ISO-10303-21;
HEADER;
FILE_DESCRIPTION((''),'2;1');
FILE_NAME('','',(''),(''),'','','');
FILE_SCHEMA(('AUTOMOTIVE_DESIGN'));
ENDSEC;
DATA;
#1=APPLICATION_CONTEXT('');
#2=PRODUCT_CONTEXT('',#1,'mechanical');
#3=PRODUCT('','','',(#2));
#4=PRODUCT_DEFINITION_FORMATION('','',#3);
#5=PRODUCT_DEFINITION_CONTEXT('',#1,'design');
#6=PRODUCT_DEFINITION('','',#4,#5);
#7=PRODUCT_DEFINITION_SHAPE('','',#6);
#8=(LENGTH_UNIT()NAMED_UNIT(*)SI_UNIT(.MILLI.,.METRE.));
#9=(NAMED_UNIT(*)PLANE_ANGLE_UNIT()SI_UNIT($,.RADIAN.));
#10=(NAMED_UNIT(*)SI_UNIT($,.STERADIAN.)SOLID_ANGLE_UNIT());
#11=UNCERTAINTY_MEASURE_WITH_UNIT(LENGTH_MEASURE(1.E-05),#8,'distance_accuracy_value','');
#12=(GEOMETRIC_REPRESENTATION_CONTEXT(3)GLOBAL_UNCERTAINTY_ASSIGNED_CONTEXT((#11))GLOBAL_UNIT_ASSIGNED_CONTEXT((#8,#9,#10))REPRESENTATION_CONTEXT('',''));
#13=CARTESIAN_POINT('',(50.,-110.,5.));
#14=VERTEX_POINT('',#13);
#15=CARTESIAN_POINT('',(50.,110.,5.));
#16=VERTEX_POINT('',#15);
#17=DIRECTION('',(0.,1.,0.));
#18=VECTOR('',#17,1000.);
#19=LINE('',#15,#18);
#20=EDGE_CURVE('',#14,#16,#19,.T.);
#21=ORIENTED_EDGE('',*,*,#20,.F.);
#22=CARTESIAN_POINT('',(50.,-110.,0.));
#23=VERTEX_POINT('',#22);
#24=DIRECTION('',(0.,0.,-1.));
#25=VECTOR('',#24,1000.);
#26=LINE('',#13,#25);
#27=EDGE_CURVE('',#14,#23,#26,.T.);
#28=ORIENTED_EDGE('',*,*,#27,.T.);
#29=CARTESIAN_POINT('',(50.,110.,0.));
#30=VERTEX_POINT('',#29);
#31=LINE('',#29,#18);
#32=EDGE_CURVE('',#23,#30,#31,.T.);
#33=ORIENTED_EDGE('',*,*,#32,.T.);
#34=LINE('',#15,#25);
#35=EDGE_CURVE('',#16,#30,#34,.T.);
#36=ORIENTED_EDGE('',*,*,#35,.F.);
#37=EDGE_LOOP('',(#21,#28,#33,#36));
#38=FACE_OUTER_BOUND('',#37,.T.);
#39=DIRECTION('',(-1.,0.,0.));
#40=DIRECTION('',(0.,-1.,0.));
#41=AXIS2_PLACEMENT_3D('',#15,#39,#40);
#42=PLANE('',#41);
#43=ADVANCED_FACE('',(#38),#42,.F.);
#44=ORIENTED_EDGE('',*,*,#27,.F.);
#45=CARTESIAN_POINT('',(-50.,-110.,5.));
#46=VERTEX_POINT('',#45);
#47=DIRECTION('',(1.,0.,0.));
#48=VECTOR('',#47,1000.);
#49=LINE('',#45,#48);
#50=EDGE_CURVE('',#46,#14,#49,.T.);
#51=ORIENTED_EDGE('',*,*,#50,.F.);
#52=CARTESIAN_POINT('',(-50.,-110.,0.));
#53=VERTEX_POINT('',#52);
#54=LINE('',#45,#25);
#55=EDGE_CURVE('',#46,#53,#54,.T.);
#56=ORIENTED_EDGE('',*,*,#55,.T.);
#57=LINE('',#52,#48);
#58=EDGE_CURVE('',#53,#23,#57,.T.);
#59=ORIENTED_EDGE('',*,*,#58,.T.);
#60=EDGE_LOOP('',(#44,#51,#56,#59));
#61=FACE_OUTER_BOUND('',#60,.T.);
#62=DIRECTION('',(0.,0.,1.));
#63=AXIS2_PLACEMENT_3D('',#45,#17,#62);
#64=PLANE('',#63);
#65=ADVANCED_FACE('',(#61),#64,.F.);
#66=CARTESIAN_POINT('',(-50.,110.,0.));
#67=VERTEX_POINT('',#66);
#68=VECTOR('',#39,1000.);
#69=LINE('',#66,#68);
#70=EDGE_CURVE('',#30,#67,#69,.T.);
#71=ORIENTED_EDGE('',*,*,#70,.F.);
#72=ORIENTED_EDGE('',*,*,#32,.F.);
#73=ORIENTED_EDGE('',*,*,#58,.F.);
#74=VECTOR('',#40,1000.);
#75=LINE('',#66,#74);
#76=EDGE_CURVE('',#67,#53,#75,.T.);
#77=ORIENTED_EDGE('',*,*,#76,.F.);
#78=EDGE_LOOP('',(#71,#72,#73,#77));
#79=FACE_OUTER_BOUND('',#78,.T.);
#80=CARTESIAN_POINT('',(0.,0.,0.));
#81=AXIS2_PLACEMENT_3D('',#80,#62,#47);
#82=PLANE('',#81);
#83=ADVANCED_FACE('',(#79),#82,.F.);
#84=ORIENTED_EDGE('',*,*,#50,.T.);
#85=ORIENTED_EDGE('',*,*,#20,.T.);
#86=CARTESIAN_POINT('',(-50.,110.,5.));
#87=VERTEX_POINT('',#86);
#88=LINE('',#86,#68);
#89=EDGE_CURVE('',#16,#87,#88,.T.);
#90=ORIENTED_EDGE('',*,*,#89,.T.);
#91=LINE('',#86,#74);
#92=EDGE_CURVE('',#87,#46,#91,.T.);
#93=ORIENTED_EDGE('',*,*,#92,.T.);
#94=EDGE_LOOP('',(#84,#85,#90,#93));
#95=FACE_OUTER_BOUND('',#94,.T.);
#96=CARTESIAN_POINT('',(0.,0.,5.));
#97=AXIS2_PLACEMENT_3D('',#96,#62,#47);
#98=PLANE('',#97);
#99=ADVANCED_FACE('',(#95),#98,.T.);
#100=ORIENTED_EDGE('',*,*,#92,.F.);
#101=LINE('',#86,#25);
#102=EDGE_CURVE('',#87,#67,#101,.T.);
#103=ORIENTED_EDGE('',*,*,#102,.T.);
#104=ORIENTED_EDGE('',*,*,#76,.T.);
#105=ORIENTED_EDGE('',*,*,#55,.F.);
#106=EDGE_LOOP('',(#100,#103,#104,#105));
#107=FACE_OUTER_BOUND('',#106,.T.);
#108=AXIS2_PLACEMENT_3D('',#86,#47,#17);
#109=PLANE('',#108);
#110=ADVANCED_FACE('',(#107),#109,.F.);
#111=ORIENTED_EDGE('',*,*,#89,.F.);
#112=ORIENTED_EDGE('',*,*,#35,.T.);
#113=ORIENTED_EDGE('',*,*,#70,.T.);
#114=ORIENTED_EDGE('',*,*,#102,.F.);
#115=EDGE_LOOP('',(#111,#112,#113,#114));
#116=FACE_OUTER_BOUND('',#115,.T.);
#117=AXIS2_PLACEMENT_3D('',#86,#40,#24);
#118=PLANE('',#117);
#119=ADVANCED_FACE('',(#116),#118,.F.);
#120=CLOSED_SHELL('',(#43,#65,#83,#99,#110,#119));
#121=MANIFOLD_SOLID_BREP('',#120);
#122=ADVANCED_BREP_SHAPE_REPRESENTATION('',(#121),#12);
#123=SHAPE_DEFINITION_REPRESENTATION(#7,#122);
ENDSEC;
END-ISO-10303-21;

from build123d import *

# Parameters (mm, degrees)
SKETCH_1_W      = 100
SKETCH_1_H      = 220
EXTRUDE_1_DEPTH = 5


with BuildPart() as part:
    # 草图1 → 凸台-拉伸1 (new body)
    with BuildSketch(Plane.XY):
        Rectangle(SKETCH_1_W, SKETCH_1_H)
    extrude(amount=EXTRUDE_1_DEPTH)


solid = part.part
